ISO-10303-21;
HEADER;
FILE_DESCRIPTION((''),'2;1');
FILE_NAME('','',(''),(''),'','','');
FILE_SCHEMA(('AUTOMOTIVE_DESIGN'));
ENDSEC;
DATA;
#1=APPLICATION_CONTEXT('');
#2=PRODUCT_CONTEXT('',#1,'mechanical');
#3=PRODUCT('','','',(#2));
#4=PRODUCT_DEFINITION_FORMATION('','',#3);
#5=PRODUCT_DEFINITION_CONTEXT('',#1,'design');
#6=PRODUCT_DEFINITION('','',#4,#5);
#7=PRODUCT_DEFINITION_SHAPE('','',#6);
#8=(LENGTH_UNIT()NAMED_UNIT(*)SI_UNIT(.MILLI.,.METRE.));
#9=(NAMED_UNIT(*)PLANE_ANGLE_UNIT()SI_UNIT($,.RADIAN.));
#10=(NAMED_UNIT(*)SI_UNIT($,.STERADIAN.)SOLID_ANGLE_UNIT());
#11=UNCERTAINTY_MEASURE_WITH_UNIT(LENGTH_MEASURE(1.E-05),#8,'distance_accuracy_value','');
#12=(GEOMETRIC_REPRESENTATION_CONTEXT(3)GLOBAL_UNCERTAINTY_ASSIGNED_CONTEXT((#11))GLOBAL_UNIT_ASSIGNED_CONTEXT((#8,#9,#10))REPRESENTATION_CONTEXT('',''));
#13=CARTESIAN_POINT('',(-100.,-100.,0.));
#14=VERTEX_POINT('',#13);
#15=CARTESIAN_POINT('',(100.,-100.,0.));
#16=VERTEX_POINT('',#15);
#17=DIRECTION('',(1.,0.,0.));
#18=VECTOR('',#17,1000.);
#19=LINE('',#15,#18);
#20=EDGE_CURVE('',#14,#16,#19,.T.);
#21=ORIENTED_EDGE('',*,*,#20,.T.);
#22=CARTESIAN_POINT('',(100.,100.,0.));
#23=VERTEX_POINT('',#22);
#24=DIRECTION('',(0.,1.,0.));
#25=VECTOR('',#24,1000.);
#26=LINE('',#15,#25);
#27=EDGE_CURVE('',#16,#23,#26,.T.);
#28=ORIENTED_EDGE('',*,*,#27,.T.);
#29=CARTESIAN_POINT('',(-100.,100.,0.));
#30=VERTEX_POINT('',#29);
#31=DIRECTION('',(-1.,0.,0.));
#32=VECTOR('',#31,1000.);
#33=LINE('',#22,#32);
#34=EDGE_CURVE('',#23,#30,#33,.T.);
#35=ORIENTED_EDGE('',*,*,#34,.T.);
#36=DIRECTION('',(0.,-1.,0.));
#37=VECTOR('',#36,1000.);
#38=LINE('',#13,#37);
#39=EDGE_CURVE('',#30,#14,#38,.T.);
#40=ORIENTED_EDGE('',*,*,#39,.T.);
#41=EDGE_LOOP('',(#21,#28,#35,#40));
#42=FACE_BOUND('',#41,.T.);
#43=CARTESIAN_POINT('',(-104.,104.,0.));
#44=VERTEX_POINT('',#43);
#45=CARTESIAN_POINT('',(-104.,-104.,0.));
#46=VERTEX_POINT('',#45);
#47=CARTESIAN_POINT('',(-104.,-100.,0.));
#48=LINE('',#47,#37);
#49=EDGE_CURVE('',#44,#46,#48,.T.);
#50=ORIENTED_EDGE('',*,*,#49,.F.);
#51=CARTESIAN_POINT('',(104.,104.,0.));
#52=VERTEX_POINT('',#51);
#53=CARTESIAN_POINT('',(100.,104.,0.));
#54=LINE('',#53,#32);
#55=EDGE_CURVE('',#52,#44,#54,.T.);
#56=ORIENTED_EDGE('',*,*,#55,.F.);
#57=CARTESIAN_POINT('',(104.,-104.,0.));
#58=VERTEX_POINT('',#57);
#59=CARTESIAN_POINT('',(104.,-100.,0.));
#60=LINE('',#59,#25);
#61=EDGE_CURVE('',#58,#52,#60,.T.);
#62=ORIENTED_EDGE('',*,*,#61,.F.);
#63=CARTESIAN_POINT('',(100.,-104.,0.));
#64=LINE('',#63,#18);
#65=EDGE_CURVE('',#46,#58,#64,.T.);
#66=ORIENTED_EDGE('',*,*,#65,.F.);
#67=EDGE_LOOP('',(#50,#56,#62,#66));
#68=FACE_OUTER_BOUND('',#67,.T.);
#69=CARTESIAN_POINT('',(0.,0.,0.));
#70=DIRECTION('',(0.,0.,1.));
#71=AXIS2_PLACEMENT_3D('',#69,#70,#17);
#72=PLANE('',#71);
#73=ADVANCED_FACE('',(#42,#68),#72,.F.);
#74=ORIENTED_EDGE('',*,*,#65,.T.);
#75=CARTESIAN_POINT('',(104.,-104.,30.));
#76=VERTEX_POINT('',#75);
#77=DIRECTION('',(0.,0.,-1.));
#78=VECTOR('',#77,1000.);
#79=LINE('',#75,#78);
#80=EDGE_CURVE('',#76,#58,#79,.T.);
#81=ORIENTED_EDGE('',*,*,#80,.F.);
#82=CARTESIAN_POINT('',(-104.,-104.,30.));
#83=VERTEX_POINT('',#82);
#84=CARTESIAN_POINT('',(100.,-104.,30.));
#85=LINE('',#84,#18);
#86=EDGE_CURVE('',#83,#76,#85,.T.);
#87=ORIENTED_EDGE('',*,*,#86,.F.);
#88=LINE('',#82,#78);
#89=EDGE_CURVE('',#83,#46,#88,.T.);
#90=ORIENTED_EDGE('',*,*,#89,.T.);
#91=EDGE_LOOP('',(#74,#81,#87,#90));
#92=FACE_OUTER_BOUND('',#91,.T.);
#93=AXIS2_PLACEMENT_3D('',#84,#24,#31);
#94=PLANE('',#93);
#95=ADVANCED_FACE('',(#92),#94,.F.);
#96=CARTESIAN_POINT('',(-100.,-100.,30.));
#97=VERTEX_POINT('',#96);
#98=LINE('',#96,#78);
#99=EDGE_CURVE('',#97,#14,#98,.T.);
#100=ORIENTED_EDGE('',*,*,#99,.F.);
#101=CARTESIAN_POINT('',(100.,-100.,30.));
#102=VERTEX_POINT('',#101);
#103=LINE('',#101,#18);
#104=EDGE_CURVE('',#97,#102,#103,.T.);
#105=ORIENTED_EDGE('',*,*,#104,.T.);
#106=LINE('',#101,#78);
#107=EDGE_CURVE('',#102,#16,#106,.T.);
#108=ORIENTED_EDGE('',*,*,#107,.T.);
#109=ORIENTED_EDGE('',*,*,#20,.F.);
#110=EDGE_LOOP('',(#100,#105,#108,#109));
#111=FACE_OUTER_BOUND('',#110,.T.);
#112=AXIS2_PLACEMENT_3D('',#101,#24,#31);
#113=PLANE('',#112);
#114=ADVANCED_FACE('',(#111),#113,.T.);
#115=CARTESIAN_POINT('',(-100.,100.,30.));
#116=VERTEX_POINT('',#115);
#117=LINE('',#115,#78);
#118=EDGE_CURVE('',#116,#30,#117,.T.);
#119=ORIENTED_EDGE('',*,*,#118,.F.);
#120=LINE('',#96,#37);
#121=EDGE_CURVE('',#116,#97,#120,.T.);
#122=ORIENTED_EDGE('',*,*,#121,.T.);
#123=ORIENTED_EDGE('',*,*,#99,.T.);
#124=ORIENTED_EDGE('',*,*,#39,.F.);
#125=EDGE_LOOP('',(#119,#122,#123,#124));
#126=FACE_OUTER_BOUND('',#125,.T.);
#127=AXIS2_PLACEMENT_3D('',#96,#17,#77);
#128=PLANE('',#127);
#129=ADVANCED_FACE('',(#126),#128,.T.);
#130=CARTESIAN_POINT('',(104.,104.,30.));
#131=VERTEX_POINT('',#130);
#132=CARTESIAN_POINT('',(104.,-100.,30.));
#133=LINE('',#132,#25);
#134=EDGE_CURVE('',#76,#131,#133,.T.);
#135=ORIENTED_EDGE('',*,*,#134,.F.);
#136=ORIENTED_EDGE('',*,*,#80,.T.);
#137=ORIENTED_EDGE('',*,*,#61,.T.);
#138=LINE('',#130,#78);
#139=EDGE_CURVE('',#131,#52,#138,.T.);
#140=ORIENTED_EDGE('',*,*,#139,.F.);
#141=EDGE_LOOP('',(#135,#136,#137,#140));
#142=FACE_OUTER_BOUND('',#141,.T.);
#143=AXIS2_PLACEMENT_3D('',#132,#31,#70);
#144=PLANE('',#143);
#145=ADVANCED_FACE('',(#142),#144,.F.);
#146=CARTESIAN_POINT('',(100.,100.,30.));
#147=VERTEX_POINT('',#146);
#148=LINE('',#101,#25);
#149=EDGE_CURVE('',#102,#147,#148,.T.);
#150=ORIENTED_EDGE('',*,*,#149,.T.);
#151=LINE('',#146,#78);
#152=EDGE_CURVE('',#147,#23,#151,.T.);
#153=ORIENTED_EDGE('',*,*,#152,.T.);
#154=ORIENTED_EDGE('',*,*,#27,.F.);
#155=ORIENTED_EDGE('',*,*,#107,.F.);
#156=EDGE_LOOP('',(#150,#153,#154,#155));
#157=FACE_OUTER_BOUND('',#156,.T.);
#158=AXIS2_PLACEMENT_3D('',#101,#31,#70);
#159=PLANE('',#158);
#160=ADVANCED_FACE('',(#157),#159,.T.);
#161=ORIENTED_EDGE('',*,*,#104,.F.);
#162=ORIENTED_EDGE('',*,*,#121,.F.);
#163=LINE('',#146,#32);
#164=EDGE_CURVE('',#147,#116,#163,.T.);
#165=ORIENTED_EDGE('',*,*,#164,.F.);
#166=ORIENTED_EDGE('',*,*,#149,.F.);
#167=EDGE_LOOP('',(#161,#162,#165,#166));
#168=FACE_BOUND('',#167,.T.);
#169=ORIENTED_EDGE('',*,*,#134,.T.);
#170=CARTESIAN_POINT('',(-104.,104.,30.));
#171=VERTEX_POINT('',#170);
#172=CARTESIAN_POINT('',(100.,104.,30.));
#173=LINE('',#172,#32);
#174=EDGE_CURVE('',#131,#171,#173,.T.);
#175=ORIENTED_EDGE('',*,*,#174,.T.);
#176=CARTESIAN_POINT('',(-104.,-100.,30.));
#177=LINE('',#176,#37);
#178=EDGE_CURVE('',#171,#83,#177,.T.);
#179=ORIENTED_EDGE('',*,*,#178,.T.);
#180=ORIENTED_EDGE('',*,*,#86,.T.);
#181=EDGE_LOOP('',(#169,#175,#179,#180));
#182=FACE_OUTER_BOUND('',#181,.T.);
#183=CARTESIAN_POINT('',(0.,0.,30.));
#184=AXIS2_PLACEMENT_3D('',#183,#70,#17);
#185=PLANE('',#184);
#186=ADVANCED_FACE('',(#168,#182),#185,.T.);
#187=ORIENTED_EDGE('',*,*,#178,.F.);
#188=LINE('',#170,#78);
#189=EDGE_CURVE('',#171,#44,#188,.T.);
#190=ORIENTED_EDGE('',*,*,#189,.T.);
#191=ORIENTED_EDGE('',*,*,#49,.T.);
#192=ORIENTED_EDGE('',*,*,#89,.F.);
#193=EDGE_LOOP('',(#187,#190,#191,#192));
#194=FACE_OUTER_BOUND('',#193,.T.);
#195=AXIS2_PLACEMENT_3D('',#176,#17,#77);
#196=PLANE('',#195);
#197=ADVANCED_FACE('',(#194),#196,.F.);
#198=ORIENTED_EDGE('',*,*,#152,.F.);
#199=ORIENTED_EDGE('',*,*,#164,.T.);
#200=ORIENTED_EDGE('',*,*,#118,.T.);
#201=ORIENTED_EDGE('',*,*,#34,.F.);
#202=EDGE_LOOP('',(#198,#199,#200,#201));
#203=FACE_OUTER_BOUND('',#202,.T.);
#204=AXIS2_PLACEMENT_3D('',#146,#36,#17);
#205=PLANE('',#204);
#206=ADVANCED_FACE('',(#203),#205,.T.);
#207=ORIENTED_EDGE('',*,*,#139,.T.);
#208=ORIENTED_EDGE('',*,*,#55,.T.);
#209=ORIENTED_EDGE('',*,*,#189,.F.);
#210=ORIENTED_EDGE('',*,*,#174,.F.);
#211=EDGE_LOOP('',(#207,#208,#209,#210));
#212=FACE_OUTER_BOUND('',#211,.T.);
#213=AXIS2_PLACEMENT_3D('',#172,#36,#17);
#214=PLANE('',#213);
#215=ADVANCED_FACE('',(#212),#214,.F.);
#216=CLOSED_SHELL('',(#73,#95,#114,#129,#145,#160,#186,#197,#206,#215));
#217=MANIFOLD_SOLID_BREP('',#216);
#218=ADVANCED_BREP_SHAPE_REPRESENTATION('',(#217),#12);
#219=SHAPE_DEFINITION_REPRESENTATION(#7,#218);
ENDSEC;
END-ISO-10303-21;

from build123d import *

# Parameters (mm, degrees)
SKETCH_1_W      = 208
SKETCH_1_H      = 208
SKETCH_1_W_2    = 200
SKETCH_1_H_2    = 200
EXTRUDE_1_DEPTH = 30


with BuildPart() as part:
    # 草图1 → 拉伸-薄壁1 (new body)
    with BuildSketch(Plane.XY):
        Rectangle(SKETCH_1_W, SKETCH_1_H)
        Rectangle(SKETCH_1_W_2, SKETCH_1_H_2, mode=Mode.SUBTRACT)
    extrude(amount=EXTRUDE_1_DEPTH)


solid = part.part
